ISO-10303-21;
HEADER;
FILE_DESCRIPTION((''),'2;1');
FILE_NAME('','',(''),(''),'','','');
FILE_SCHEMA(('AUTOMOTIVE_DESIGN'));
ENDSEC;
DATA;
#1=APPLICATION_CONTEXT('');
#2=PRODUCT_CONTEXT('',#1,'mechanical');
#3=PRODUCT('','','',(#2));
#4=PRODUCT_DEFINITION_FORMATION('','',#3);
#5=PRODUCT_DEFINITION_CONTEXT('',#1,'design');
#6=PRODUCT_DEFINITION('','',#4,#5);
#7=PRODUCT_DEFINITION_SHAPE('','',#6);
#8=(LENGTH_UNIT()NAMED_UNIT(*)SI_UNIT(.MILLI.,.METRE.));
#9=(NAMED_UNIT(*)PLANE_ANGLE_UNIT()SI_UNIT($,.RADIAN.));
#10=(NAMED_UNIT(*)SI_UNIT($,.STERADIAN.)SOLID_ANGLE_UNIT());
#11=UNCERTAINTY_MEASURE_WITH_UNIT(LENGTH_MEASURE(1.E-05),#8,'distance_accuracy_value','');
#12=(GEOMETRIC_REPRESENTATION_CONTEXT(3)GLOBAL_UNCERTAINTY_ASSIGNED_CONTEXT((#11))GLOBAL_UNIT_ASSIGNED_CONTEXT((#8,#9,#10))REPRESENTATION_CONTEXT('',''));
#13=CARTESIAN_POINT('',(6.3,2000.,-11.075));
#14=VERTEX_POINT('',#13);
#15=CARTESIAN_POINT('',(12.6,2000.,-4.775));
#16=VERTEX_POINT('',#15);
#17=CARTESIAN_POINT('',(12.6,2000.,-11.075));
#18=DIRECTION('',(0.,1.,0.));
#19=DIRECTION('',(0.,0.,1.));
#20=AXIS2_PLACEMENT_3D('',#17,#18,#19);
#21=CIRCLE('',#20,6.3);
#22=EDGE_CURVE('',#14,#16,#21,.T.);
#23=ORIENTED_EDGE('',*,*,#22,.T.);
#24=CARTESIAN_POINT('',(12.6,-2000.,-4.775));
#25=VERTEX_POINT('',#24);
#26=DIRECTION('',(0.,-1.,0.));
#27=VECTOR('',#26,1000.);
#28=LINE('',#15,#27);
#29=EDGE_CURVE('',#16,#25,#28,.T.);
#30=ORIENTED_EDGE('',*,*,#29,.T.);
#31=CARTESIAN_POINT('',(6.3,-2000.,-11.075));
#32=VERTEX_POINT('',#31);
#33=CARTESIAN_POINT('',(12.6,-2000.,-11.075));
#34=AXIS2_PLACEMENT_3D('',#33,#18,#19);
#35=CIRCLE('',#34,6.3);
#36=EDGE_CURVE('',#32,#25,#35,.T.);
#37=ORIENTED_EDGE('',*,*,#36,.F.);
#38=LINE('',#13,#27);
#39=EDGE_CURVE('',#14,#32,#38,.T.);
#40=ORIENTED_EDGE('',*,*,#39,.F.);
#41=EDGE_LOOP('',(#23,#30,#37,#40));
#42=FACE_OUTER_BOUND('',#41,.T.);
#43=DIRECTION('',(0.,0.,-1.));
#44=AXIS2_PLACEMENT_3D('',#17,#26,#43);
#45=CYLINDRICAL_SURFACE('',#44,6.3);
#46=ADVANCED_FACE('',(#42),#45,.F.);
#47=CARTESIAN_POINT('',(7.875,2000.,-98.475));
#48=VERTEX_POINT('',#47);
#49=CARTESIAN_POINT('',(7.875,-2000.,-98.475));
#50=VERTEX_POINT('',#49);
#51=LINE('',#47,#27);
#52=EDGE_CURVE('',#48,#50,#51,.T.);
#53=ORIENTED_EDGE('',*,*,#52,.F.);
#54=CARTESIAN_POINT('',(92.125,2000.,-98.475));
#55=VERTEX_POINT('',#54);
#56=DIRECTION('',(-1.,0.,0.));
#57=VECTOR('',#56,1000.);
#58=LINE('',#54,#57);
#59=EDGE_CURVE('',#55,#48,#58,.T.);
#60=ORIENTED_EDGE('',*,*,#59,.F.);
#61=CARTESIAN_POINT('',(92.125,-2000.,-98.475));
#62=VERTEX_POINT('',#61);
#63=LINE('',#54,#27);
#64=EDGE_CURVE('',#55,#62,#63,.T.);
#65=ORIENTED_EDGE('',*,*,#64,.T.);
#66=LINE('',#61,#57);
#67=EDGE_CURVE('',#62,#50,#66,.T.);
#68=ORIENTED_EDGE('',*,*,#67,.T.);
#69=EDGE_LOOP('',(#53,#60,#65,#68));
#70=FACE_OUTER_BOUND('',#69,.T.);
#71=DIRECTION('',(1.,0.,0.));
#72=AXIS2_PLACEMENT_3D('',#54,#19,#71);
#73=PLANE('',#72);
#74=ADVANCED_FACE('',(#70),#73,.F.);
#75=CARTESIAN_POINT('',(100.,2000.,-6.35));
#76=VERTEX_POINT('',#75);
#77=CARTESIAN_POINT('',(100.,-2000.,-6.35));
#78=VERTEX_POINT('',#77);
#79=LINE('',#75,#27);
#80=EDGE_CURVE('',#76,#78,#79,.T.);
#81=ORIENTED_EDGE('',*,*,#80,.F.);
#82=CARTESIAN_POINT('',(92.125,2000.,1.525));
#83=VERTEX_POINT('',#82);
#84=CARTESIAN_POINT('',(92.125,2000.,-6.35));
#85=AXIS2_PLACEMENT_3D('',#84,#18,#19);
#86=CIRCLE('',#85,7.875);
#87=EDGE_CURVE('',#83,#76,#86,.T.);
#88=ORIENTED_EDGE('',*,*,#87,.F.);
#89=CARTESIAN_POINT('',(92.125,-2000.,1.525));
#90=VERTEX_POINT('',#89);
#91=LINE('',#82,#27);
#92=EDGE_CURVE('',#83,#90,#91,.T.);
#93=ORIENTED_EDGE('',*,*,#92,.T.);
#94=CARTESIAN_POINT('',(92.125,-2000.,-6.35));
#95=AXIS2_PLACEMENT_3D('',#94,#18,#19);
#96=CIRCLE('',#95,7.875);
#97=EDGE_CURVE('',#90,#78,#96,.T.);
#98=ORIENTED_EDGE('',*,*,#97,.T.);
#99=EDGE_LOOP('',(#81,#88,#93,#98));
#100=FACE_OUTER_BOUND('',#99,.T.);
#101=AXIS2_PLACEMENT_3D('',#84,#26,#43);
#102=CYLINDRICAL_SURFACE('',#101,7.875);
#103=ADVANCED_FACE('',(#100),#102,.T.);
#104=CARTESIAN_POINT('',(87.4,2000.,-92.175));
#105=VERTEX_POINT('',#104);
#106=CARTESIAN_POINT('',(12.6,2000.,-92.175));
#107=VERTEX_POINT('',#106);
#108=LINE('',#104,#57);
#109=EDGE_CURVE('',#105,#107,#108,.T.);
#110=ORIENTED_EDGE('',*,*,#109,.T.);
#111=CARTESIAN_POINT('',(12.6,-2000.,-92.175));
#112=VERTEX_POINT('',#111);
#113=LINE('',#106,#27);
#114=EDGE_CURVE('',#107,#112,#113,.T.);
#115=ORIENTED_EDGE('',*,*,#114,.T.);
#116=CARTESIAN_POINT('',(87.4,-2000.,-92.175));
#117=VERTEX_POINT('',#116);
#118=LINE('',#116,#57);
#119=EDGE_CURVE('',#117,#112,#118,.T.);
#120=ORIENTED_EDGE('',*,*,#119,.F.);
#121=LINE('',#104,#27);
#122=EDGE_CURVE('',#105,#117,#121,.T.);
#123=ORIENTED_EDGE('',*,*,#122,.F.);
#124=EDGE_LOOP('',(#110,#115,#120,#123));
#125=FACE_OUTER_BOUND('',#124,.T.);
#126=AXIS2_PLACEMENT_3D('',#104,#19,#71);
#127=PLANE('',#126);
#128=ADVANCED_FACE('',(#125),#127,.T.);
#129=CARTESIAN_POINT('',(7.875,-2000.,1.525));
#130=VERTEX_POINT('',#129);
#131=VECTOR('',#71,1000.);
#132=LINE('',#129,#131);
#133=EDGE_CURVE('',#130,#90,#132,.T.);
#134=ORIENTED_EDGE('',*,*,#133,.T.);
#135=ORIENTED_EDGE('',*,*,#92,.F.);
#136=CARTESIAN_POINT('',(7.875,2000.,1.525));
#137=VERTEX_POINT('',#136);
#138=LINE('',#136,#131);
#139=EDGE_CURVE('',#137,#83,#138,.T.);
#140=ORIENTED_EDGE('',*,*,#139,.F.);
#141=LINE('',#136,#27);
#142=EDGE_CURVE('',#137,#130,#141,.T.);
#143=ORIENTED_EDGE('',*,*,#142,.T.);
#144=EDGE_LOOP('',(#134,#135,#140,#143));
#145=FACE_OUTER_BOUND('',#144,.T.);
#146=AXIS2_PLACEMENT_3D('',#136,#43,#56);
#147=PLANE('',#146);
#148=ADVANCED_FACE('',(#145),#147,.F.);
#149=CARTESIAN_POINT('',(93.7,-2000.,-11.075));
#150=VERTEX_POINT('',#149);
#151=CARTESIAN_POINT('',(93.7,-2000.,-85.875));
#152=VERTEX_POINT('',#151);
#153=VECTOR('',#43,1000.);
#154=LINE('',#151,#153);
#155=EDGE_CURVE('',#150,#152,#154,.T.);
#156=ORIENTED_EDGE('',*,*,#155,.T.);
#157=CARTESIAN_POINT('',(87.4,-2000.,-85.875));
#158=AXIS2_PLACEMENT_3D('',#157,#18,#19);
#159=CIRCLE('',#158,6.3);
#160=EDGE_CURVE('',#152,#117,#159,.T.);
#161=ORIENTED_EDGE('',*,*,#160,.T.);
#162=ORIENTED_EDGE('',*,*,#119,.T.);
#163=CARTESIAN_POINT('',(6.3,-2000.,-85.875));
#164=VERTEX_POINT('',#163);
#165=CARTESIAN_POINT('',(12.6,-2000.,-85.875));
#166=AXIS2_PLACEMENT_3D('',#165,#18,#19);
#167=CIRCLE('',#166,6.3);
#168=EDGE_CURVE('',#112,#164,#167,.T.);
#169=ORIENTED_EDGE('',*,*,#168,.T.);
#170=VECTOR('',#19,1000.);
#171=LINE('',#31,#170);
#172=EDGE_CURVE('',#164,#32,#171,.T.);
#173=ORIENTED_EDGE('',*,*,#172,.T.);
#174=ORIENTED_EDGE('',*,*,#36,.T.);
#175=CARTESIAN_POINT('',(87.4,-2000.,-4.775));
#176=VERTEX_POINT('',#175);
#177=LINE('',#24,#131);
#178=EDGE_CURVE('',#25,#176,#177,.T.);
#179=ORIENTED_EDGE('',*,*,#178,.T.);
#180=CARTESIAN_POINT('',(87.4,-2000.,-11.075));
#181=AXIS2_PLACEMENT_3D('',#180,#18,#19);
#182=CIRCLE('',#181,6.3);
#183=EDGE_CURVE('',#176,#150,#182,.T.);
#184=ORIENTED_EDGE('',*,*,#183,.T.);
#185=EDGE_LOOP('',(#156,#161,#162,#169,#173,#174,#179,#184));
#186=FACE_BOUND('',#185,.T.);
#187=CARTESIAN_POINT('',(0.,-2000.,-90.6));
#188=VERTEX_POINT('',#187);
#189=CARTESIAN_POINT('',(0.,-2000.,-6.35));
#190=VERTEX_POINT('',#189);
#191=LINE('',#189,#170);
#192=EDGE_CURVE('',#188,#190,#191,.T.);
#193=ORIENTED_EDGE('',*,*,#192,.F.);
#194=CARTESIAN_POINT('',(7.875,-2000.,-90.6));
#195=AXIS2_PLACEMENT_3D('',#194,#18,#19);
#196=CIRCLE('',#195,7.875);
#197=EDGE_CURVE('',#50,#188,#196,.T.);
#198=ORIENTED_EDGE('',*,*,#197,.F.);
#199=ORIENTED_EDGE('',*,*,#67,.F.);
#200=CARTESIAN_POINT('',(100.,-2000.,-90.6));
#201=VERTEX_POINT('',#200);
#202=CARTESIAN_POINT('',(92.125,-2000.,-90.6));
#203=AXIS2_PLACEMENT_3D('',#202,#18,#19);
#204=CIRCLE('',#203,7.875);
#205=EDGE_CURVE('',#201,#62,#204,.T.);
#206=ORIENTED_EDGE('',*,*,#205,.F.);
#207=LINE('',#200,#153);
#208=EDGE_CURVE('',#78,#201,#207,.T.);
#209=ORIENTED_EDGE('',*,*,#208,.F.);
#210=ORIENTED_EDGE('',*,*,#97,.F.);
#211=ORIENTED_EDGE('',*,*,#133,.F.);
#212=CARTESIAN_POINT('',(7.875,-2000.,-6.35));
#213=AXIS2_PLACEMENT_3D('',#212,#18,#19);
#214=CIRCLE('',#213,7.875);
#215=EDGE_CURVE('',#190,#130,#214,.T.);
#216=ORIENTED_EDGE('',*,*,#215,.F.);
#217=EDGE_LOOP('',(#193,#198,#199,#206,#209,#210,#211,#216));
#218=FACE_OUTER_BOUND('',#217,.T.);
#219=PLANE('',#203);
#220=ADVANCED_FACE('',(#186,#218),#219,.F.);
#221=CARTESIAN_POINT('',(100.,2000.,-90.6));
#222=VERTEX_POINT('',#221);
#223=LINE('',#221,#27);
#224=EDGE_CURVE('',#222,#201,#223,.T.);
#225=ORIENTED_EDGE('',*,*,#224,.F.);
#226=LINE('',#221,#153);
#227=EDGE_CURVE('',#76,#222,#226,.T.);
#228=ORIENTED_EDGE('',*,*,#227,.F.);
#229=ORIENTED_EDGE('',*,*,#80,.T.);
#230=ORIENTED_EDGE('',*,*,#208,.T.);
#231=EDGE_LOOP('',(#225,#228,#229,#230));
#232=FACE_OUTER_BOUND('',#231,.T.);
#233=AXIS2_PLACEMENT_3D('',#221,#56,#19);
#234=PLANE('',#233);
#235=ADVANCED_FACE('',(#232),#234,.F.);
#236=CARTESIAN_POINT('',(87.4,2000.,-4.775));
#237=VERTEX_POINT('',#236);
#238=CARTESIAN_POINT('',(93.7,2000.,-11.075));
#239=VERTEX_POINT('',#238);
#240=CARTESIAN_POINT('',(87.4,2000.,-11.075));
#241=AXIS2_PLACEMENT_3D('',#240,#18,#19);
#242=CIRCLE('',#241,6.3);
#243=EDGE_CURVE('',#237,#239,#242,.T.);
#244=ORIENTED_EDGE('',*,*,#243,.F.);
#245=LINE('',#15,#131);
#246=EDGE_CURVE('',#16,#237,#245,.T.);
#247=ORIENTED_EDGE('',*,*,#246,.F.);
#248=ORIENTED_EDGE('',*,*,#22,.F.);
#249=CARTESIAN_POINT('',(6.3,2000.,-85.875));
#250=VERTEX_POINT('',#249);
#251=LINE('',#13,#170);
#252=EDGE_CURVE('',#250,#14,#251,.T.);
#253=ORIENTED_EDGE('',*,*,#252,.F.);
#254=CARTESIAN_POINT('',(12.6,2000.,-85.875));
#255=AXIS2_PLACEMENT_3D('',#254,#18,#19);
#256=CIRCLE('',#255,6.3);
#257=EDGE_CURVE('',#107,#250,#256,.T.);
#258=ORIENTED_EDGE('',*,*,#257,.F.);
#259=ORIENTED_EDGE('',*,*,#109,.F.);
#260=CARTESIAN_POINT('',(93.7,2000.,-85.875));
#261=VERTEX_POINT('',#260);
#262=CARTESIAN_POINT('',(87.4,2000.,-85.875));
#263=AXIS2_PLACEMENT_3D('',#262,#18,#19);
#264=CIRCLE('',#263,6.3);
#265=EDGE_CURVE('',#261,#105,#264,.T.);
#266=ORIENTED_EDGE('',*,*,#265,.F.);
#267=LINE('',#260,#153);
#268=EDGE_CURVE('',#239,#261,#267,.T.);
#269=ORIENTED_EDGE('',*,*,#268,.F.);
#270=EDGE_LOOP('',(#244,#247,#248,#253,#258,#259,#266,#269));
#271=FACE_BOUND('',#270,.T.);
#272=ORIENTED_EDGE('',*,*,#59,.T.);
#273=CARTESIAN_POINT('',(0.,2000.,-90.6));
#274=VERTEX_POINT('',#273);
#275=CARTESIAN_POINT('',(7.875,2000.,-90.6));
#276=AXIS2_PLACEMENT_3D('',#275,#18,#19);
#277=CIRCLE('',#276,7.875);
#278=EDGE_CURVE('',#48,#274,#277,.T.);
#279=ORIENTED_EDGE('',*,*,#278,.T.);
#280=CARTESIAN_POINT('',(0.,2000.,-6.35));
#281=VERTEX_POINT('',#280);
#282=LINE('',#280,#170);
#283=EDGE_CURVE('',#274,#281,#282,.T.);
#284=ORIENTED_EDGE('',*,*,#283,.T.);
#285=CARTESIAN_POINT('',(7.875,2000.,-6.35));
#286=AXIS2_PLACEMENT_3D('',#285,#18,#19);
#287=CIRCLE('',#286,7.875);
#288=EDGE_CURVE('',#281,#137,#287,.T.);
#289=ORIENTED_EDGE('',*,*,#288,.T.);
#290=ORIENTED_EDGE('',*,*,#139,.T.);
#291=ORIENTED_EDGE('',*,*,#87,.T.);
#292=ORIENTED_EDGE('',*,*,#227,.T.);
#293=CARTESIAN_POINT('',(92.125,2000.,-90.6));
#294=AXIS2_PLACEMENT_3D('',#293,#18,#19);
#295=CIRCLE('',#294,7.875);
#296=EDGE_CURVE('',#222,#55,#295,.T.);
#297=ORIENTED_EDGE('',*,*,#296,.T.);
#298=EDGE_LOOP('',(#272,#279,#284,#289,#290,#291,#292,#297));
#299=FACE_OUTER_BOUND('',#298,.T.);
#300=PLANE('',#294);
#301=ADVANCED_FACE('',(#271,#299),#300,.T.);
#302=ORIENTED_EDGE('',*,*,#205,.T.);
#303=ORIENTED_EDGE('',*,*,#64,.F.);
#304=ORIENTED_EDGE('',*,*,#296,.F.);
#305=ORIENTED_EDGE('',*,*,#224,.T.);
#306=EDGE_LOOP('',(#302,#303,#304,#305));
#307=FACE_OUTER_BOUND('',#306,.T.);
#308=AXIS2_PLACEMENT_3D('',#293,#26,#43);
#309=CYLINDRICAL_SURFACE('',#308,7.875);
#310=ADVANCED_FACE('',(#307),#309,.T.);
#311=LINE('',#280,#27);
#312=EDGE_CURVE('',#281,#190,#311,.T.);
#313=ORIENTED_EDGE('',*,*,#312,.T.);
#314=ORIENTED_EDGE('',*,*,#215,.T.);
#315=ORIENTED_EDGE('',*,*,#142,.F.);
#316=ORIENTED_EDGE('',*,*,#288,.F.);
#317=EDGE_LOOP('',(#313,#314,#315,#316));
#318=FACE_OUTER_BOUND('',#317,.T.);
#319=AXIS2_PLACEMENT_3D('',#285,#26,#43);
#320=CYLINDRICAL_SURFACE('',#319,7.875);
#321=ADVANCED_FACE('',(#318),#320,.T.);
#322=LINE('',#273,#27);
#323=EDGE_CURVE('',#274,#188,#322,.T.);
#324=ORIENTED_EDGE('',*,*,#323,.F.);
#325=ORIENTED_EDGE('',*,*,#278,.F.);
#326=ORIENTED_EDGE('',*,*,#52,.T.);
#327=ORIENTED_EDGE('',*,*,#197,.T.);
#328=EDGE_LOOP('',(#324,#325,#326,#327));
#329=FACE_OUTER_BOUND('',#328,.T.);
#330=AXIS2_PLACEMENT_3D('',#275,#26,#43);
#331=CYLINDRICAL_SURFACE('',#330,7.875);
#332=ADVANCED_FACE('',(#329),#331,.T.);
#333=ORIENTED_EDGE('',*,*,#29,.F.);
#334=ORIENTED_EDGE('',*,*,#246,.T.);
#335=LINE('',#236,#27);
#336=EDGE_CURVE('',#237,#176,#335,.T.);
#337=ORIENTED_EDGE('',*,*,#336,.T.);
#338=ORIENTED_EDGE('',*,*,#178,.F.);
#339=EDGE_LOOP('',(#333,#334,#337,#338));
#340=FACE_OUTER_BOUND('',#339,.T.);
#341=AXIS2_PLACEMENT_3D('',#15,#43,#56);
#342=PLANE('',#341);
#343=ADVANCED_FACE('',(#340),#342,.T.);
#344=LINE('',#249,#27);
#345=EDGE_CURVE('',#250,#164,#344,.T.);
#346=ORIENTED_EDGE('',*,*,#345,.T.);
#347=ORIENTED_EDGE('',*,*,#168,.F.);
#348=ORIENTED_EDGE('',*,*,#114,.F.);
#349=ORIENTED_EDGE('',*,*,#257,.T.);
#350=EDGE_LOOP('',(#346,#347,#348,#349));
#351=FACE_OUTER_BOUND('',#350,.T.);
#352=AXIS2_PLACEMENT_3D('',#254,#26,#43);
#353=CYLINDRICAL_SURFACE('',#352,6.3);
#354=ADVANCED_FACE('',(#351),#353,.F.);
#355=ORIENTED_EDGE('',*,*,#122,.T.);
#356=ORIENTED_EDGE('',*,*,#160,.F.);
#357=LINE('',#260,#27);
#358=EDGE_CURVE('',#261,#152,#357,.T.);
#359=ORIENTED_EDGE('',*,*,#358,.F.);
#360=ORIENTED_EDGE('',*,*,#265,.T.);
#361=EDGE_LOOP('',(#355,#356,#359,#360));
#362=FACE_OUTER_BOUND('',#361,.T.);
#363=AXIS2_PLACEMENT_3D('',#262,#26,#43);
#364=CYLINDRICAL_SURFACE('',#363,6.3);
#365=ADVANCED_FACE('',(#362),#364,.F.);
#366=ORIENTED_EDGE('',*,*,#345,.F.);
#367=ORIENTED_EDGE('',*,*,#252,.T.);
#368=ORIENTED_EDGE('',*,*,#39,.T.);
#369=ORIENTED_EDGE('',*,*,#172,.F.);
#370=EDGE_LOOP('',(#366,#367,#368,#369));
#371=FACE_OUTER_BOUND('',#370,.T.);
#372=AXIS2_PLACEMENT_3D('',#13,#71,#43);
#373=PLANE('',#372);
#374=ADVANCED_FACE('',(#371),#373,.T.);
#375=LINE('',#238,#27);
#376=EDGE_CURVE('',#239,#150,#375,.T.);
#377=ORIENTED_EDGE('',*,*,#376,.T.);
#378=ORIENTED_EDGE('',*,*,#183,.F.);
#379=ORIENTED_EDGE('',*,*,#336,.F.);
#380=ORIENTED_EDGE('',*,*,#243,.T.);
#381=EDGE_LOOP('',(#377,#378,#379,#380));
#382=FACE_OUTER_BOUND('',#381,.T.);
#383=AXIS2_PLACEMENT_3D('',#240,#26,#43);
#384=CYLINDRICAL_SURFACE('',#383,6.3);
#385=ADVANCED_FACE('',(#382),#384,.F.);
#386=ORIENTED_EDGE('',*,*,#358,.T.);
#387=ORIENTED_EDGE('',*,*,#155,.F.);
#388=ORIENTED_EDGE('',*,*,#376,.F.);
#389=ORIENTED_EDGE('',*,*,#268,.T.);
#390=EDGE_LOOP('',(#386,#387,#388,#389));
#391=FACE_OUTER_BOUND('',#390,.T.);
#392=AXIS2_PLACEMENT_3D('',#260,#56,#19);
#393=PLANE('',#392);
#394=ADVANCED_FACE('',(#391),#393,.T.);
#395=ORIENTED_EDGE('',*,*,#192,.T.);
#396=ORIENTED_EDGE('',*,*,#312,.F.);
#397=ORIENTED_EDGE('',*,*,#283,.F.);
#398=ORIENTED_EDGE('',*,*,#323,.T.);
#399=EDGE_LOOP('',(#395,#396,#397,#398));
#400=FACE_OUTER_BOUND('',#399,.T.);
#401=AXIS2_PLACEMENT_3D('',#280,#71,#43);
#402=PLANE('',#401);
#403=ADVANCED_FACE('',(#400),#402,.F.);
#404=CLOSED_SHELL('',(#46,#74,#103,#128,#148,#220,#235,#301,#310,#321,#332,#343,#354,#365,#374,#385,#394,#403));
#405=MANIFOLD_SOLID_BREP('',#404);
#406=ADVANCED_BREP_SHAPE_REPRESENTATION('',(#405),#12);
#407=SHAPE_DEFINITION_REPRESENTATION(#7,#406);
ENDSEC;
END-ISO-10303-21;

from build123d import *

# Parameters (mm, degrees)
BOSS_EXTRUDE1_DEPTH = 2000


with BuildPart() as part:
    # Sketch2 → Boss-Extrude1 (new, symmetric)
    with BuildSketch(Plane(origin=(0, 0, 0), x_dir=(1, 0, 0), z_dir=(0, 1, 0))):
        with BuildLine():
            Line((7.875, -1.525), (92.125, -1.525))
            ThreePointArc((92.125, -1.525), (97.693465902, 0.781534098), (100, 6.35))
            Line((100, 6.35), (100, 90.6))
            ThreePointArc((100, 90.6), (97.693465902, 96.168465902), (92.125, 98.475))
            Line((92.125, 98.475), (7.875, 98.475))
            ThreePointArc((7.875, 98.475), (2.306534098, 96.168465902), (0, 90.6))
            Line((0, 90.6), (0, 6.35))
            ThreePointArc((0, 6.35), (2.306534098, 0.781534098), (7.875, -1.525))
        make_face()
        with BuildLine():
            Line((12.6, 4.775), (87.4, 4.775))
            ThreePointArc((87.4, 4.775), (91.854772721, 6.620227279), (93.7, 11.075))
            Line((93.7, 11.075), (93.7, 85.875))
            ThreePointArc((93.7, 85.875), (91.854772721, 90.329772721), (87.4, 92.175))
            Line((87.4, 92.175), (12.6, 92.175))
            ThreePointArc((12.6, 92.175), (8.145227279, 90.329772721), (6.3, 85.875))
            Line((6.3, 85.875), (6.3, 11.075))
            ThreePointArc((6.3, 11.075), (8.145227279, 6.620227279), (12.6, 4.775))
        make_face(mode=Mode.SUBTRACT)
    extrude(amount=BOSS_EXTRUDE1_DEPTH, both=True)


solid = part.part
